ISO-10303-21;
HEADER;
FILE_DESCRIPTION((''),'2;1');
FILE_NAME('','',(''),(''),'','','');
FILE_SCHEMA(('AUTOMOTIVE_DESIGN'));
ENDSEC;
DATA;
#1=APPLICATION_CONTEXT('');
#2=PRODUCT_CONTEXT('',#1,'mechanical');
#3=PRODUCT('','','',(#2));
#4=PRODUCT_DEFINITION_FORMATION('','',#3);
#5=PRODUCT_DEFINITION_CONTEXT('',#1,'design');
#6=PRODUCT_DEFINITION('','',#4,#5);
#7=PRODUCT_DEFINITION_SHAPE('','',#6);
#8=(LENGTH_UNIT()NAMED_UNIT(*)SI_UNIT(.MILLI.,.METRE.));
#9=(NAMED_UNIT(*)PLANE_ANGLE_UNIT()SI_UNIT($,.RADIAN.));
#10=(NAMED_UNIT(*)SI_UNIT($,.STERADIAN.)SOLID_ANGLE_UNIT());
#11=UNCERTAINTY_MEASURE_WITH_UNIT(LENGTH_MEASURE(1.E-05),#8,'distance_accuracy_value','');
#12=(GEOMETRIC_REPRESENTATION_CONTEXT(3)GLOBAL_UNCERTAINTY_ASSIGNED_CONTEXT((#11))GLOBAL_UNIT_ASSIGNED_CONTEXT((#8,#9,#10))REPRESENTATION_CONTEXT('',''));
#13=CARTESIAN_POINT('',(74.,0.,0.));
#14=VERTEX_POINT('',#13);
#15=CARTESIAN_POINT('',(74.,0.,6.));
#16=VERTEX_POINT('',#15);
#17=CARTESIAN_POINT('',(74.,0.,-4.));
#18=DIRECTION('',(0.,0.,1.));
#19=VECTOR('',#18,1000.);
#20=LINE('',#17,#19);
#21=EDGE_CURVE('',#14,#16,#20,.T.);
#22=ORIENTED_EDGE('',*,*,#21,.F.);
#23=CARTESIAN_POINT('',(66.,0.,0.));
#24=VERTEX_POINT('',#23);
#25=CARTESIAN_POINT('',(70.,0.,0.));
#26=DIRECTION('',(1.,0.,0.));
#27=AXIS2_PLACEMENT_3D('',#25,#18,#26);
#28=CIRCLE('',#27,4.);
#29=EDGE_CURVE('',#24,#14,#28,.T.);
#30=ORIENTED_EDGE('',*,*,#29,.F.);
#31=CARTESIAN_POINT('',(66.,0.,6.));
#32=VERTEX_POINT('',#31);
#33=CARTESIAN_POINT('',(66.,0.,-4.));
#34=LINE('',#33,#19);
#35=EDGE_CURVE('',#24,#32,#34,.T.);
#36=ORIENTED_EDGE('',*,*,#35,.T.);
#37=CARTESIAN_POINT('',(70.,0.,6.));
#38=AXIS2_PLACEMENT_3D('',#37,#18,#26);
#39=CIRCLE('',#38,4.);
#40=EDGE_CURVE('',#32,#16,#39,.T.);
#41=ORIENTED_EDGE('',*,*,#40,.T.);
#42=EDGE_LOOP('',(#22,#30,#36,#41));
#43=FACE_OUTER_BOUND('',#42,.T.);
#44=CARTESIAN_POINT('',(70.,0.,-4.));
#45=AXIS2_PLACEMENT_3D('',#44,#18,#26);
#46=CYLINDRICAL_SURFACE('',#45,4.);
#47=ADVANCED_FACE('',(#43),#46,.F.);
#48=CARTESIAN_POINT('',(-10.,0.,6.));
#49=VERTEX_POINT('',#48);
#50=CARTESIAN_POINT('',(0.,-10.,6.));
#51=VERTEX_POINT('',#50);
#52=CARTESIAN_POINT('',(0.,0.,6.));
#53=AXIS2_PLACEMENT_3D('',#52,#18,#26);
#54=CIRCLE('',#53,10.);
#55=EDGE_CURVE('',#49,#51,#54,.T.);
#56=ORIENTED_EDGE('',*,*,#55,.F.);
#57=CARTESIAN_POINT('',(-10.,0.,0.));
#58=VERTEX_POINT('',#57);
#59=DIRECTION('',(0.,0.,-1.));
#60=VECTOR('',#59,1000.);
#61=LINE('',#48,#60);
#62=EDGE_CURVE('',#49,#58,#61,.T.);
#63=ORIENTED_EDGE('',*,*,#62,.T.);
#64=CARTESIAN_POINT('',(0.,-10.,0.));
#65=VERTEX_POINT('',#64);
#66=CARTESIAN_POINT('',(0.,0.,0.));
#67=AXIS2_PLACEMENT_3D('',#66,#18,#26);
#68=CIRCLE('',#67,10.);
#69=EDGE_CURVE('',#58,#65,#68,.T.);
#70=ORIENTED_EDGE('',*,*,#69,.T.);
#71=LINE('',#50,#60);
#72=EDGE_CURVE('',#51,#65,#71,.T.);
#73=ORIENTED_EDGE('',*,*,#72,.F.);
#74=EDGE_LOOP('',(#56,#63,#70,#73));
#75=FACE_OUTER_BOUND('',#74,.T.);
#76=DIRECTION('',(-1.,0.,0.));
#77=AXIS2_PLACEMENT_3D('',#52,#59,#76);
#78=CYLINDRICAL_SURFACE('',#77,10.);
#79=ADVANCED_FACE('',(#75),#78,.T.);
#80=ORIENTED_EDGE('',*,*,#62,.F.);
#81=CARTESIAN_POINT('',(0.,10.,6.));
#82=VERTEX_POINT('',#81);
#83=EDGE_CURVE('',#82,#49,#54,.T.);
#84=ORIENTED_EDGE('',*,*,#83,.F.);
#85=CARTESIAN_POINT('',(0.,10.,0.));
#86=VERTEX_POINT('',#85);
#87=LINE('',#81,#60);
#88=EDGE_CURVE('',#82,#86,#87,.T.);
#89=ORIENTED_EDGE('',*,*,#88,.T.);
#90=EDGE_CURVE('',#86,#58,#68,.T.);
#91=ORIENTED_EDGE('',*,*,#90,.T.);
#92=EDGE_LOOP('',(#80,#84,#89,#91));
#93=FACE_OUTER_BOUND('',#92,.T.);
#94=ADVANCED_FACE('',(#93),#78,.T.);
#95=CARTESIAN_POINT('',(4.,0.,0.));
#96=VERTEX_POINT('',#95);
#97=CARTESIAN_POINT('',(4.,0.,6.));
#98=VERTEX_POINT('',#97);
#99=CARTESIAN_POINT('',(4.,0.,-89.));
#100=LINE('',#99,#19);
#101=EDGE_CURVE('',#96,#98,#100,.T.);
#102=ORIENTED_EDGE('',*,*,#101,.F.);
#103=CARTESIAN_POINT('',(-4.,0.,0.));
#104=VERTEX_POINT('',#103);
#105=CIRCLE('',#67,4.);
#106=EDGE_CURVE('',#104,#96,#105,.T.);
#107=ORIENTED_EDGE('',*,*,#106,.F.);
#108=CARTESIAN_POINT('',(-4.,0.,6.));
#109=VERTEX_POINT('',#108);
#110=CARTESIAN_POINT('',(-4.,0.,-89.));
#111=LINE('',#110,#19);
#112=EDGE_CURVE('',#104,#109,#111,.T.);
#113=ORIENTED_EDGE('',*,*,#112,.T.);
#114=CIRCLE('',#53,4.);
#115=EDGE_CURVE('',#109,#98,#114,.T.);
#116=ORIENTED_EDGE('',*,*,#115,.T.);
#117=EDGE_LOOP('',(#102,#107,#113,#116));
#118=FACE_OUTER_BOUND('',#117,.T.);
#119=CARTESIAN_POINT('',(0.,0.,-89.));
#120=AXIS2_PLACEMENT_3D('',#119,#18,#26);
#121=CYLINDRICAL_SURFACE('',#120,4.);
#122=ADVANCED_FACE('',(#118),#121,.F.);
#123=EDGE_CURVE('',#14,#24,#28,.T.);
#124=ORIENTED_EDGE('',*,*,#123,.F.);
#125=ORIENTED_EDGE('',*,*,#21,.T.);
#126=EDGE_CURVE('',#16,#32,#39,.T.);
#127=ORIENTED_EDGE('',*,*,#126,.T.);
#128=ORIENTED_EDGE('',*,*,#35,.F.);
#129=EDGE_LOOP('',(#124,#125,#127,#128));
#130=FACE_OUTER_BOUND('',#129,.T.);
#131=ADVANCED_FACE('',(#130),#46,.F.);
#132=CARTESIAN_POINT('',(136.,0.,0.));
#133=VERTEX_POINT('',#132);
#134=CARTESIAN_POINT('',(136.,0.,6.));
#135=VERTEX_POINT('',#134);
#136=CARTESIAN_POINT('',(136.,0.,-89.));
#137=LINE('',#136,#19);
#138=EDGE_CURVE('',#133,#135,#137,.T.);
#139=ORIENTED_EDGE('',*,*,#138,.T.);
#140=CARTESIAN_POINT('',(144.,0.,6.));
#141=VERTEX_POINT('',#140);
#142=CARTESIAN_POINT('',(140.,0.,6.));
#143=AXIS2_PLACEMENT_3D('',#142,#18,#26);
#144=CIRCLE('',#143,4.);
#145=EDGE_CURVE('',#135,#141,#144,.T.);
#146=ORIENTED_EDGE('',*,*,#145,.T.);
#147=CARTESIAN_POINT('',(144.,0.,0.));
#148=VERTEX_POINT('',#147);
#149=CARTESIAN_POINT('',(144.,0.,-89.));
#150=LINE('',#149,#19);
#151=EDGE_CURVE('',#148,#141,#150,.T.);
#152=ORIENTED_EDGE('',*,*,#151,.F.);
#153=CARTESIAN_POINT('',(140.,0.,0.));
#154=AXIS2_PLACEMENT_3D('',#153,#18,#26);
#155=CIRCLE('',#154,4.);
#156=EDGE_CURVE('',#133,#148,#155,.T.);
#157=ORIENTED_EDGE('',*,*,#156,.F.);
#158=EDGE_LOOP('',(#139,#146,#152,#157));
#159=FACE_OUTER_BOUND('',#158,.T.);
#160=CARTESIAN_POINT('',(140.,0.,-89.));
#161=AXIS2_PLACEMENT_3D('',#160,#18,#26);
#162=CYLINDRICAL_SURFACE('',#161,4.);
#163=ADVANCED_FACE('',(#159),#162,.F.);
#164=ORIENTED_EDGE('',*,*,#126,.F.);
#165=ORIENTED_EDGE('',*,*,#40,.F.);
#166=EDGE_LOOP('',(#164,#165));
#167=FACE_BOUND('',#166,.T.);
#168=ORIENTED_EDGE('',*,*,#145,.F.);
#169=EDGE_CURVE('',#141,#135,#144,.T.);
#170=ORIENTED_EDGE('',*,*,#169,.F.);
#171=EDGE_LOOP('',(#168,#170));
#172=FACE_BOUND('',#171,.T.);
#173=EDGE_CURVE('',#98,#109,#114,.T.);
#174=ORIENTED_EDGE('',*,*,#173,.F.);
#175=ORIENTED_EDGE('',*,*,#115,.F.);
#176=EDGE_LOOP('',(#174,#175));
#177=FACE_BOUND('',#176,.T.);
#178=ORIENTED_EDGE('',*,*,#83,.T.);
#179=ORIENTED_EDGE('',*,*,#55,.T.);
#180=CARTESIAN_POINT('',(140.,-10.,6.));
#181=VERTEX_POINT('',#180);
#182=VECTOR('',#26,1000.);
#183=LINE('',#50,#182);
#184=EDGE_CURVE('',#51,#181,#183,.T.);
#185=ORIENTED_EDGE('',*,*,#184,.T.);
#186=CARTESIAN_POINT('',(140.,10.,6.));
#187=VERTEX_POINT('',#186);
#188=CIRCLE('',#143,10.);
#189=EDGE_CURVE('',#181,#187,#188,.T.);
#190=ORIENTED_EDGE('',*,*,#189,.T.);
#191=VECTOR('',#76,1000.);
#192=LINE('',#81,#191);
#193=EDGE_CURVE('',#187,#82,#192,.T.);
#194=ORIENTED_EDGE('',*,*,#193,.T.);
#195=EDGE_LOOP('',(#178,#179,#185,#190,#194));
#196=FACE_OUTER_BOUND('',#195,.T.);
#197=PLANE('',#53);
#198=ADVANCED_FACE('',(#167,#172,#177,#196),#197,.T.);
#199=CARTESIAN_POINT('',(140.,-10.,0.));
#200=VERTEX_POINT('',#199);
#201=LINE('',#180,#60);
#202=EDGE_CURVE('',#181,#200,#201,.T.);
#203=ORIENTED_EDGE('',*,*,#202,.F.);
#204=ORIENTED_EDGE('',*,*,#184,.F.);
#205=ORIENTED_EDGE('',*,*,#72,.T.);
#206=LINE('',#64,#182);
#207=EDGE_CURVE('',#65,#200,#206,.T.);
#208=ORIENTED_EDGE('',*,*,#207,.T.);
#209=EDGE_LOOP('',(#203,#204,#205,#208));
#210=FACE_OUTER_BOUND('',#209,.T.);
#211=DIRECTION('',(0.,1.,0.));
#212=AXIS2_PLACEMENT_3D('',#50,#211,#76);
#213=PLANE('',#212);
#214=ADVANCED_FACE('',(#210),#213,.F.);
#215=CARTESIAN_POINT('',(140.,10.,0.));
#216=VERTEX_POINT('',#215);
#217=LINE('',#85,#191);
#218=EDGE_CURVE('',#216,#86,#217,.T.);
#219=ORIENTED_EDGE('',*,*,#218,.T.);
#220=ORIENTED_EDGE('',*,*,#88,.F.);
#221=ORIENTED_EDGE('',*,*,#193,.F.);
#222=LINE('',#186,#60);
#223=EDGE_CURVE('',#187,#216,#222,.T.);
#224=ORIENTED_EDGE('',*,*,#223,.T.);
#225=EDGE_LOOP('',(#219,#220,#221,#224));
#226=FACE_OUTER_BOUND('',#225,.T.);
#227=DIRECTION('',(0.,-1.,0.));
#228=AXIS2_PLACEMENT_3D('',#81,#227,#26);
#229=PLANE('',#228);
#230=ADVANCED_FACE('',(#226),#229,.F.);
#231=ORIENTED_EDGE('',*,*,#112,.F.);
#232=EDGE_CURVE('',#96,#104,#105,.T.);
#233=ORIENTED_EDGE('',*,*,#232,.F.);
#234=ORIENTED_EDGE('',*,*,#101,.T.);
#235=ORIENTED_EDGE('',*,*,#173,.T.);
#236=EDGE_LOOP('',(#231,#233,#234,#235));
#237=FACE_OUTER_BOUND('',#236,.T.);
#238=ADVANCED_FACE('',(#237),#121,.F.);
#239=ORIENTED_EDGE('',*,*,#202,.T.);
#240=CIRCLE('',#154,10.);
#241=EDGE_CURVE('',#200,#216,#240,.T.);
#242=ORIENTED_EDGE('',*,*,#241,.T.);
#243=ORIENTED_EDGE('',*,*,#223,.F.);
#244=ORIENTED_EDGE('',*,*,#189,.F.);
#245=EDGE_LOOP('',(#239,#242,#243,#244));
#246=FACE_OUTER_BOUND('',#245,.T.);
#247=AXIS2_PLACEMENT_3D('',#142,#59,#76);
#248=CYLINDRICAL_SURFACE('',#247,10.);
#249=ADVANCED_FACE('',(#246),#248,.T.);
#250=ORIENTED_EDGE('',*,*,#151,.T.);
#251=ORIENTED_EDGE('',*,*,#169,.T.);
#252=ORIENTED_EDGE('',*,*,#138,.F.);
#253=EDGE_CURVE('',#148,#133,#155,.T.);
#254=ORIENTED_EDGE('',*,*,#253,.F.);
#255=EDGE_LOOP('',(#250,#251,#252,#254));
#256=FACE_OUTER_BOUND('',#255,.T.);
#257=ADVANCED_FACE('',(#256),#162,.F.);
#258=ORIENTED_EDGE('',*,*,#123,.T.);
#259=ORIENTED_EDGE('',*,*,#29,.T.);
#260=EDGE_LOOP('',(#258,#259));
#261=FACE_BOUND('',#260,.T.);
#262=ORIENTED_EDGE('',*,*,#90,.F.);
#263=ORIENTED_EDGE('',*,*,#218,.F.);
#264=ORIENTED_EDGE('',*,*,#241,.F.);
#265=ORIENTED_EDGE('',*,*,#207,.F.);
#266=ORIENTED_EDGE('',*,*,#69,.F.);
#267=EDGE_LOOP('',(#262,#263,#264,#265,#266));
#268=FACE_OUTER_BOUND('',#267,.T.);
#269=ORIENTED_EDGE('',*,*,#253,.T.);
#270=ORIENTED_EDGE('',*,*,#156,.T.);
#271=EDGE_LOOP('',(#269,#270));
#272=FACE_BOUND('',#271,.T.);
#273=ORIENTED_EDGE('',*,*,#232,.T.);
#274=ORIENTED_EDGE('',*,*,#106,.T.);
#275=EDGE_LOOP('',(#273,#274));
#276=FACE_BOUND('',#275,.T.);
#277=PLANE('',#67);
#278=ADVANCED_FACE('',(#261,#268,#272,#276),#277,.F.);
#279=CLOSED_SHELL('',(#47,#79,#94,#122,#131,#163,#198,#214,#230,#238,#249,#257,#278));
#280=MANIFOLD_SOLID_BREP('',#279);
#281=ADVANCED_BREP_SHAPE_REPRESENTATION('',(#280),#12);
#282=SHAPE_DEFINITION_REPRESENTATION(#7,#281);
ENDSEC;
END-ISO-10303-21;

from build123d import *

# Parameters (mm, degrees)
BOSS_EXTRUDE1_DEPTH = 6
SKETCH2_R           = 4
CUT_EXTRUDE1_DEPTH  = 95
SKETCH3_R           = 4
CUT_EXTRUDE2_DEPTH  = 10


with BuildPart() as part:
    # Sketch1 → Boss-Extrude1 (new body)
    with BuildSketch(Plane.XY):
        with BuildLine():
            Line((0, 10), (140, 10))
            ThreePointArc((140, 10), (150, 0), (140, -10))
            Line((140, -10), (0, -10))
            ThreePointArc((0, -10), (-10, 0), (0, 10))
        make_face()
    extrude(amount=BOSS_EXTRUDE1_DEPTH)

    # Sketch2 → Cut-Extrude1 (cut)
    with BuildSketch(Plane.XY.offset(6)):
        Circle(SKETCH2_R)
        with Locations((140, 0)):
            Circle(SKETCH2_R)
    extrude(amount=-CUT_EXTRUDE1_DEPTH, mode=Mode.SUBTRACT)

    # Sketch3 → Cut-Extrude2 (cut)
    with BuildSketch(Plane.XY.offset(6)):
        with Locations((70, 0)):
            Circle(SKETCH3_R)
    extrude(amount=-CUT_EXTRUDE2_DEPTH, mode=Mode.SUBTRACT)


solid = part.part
